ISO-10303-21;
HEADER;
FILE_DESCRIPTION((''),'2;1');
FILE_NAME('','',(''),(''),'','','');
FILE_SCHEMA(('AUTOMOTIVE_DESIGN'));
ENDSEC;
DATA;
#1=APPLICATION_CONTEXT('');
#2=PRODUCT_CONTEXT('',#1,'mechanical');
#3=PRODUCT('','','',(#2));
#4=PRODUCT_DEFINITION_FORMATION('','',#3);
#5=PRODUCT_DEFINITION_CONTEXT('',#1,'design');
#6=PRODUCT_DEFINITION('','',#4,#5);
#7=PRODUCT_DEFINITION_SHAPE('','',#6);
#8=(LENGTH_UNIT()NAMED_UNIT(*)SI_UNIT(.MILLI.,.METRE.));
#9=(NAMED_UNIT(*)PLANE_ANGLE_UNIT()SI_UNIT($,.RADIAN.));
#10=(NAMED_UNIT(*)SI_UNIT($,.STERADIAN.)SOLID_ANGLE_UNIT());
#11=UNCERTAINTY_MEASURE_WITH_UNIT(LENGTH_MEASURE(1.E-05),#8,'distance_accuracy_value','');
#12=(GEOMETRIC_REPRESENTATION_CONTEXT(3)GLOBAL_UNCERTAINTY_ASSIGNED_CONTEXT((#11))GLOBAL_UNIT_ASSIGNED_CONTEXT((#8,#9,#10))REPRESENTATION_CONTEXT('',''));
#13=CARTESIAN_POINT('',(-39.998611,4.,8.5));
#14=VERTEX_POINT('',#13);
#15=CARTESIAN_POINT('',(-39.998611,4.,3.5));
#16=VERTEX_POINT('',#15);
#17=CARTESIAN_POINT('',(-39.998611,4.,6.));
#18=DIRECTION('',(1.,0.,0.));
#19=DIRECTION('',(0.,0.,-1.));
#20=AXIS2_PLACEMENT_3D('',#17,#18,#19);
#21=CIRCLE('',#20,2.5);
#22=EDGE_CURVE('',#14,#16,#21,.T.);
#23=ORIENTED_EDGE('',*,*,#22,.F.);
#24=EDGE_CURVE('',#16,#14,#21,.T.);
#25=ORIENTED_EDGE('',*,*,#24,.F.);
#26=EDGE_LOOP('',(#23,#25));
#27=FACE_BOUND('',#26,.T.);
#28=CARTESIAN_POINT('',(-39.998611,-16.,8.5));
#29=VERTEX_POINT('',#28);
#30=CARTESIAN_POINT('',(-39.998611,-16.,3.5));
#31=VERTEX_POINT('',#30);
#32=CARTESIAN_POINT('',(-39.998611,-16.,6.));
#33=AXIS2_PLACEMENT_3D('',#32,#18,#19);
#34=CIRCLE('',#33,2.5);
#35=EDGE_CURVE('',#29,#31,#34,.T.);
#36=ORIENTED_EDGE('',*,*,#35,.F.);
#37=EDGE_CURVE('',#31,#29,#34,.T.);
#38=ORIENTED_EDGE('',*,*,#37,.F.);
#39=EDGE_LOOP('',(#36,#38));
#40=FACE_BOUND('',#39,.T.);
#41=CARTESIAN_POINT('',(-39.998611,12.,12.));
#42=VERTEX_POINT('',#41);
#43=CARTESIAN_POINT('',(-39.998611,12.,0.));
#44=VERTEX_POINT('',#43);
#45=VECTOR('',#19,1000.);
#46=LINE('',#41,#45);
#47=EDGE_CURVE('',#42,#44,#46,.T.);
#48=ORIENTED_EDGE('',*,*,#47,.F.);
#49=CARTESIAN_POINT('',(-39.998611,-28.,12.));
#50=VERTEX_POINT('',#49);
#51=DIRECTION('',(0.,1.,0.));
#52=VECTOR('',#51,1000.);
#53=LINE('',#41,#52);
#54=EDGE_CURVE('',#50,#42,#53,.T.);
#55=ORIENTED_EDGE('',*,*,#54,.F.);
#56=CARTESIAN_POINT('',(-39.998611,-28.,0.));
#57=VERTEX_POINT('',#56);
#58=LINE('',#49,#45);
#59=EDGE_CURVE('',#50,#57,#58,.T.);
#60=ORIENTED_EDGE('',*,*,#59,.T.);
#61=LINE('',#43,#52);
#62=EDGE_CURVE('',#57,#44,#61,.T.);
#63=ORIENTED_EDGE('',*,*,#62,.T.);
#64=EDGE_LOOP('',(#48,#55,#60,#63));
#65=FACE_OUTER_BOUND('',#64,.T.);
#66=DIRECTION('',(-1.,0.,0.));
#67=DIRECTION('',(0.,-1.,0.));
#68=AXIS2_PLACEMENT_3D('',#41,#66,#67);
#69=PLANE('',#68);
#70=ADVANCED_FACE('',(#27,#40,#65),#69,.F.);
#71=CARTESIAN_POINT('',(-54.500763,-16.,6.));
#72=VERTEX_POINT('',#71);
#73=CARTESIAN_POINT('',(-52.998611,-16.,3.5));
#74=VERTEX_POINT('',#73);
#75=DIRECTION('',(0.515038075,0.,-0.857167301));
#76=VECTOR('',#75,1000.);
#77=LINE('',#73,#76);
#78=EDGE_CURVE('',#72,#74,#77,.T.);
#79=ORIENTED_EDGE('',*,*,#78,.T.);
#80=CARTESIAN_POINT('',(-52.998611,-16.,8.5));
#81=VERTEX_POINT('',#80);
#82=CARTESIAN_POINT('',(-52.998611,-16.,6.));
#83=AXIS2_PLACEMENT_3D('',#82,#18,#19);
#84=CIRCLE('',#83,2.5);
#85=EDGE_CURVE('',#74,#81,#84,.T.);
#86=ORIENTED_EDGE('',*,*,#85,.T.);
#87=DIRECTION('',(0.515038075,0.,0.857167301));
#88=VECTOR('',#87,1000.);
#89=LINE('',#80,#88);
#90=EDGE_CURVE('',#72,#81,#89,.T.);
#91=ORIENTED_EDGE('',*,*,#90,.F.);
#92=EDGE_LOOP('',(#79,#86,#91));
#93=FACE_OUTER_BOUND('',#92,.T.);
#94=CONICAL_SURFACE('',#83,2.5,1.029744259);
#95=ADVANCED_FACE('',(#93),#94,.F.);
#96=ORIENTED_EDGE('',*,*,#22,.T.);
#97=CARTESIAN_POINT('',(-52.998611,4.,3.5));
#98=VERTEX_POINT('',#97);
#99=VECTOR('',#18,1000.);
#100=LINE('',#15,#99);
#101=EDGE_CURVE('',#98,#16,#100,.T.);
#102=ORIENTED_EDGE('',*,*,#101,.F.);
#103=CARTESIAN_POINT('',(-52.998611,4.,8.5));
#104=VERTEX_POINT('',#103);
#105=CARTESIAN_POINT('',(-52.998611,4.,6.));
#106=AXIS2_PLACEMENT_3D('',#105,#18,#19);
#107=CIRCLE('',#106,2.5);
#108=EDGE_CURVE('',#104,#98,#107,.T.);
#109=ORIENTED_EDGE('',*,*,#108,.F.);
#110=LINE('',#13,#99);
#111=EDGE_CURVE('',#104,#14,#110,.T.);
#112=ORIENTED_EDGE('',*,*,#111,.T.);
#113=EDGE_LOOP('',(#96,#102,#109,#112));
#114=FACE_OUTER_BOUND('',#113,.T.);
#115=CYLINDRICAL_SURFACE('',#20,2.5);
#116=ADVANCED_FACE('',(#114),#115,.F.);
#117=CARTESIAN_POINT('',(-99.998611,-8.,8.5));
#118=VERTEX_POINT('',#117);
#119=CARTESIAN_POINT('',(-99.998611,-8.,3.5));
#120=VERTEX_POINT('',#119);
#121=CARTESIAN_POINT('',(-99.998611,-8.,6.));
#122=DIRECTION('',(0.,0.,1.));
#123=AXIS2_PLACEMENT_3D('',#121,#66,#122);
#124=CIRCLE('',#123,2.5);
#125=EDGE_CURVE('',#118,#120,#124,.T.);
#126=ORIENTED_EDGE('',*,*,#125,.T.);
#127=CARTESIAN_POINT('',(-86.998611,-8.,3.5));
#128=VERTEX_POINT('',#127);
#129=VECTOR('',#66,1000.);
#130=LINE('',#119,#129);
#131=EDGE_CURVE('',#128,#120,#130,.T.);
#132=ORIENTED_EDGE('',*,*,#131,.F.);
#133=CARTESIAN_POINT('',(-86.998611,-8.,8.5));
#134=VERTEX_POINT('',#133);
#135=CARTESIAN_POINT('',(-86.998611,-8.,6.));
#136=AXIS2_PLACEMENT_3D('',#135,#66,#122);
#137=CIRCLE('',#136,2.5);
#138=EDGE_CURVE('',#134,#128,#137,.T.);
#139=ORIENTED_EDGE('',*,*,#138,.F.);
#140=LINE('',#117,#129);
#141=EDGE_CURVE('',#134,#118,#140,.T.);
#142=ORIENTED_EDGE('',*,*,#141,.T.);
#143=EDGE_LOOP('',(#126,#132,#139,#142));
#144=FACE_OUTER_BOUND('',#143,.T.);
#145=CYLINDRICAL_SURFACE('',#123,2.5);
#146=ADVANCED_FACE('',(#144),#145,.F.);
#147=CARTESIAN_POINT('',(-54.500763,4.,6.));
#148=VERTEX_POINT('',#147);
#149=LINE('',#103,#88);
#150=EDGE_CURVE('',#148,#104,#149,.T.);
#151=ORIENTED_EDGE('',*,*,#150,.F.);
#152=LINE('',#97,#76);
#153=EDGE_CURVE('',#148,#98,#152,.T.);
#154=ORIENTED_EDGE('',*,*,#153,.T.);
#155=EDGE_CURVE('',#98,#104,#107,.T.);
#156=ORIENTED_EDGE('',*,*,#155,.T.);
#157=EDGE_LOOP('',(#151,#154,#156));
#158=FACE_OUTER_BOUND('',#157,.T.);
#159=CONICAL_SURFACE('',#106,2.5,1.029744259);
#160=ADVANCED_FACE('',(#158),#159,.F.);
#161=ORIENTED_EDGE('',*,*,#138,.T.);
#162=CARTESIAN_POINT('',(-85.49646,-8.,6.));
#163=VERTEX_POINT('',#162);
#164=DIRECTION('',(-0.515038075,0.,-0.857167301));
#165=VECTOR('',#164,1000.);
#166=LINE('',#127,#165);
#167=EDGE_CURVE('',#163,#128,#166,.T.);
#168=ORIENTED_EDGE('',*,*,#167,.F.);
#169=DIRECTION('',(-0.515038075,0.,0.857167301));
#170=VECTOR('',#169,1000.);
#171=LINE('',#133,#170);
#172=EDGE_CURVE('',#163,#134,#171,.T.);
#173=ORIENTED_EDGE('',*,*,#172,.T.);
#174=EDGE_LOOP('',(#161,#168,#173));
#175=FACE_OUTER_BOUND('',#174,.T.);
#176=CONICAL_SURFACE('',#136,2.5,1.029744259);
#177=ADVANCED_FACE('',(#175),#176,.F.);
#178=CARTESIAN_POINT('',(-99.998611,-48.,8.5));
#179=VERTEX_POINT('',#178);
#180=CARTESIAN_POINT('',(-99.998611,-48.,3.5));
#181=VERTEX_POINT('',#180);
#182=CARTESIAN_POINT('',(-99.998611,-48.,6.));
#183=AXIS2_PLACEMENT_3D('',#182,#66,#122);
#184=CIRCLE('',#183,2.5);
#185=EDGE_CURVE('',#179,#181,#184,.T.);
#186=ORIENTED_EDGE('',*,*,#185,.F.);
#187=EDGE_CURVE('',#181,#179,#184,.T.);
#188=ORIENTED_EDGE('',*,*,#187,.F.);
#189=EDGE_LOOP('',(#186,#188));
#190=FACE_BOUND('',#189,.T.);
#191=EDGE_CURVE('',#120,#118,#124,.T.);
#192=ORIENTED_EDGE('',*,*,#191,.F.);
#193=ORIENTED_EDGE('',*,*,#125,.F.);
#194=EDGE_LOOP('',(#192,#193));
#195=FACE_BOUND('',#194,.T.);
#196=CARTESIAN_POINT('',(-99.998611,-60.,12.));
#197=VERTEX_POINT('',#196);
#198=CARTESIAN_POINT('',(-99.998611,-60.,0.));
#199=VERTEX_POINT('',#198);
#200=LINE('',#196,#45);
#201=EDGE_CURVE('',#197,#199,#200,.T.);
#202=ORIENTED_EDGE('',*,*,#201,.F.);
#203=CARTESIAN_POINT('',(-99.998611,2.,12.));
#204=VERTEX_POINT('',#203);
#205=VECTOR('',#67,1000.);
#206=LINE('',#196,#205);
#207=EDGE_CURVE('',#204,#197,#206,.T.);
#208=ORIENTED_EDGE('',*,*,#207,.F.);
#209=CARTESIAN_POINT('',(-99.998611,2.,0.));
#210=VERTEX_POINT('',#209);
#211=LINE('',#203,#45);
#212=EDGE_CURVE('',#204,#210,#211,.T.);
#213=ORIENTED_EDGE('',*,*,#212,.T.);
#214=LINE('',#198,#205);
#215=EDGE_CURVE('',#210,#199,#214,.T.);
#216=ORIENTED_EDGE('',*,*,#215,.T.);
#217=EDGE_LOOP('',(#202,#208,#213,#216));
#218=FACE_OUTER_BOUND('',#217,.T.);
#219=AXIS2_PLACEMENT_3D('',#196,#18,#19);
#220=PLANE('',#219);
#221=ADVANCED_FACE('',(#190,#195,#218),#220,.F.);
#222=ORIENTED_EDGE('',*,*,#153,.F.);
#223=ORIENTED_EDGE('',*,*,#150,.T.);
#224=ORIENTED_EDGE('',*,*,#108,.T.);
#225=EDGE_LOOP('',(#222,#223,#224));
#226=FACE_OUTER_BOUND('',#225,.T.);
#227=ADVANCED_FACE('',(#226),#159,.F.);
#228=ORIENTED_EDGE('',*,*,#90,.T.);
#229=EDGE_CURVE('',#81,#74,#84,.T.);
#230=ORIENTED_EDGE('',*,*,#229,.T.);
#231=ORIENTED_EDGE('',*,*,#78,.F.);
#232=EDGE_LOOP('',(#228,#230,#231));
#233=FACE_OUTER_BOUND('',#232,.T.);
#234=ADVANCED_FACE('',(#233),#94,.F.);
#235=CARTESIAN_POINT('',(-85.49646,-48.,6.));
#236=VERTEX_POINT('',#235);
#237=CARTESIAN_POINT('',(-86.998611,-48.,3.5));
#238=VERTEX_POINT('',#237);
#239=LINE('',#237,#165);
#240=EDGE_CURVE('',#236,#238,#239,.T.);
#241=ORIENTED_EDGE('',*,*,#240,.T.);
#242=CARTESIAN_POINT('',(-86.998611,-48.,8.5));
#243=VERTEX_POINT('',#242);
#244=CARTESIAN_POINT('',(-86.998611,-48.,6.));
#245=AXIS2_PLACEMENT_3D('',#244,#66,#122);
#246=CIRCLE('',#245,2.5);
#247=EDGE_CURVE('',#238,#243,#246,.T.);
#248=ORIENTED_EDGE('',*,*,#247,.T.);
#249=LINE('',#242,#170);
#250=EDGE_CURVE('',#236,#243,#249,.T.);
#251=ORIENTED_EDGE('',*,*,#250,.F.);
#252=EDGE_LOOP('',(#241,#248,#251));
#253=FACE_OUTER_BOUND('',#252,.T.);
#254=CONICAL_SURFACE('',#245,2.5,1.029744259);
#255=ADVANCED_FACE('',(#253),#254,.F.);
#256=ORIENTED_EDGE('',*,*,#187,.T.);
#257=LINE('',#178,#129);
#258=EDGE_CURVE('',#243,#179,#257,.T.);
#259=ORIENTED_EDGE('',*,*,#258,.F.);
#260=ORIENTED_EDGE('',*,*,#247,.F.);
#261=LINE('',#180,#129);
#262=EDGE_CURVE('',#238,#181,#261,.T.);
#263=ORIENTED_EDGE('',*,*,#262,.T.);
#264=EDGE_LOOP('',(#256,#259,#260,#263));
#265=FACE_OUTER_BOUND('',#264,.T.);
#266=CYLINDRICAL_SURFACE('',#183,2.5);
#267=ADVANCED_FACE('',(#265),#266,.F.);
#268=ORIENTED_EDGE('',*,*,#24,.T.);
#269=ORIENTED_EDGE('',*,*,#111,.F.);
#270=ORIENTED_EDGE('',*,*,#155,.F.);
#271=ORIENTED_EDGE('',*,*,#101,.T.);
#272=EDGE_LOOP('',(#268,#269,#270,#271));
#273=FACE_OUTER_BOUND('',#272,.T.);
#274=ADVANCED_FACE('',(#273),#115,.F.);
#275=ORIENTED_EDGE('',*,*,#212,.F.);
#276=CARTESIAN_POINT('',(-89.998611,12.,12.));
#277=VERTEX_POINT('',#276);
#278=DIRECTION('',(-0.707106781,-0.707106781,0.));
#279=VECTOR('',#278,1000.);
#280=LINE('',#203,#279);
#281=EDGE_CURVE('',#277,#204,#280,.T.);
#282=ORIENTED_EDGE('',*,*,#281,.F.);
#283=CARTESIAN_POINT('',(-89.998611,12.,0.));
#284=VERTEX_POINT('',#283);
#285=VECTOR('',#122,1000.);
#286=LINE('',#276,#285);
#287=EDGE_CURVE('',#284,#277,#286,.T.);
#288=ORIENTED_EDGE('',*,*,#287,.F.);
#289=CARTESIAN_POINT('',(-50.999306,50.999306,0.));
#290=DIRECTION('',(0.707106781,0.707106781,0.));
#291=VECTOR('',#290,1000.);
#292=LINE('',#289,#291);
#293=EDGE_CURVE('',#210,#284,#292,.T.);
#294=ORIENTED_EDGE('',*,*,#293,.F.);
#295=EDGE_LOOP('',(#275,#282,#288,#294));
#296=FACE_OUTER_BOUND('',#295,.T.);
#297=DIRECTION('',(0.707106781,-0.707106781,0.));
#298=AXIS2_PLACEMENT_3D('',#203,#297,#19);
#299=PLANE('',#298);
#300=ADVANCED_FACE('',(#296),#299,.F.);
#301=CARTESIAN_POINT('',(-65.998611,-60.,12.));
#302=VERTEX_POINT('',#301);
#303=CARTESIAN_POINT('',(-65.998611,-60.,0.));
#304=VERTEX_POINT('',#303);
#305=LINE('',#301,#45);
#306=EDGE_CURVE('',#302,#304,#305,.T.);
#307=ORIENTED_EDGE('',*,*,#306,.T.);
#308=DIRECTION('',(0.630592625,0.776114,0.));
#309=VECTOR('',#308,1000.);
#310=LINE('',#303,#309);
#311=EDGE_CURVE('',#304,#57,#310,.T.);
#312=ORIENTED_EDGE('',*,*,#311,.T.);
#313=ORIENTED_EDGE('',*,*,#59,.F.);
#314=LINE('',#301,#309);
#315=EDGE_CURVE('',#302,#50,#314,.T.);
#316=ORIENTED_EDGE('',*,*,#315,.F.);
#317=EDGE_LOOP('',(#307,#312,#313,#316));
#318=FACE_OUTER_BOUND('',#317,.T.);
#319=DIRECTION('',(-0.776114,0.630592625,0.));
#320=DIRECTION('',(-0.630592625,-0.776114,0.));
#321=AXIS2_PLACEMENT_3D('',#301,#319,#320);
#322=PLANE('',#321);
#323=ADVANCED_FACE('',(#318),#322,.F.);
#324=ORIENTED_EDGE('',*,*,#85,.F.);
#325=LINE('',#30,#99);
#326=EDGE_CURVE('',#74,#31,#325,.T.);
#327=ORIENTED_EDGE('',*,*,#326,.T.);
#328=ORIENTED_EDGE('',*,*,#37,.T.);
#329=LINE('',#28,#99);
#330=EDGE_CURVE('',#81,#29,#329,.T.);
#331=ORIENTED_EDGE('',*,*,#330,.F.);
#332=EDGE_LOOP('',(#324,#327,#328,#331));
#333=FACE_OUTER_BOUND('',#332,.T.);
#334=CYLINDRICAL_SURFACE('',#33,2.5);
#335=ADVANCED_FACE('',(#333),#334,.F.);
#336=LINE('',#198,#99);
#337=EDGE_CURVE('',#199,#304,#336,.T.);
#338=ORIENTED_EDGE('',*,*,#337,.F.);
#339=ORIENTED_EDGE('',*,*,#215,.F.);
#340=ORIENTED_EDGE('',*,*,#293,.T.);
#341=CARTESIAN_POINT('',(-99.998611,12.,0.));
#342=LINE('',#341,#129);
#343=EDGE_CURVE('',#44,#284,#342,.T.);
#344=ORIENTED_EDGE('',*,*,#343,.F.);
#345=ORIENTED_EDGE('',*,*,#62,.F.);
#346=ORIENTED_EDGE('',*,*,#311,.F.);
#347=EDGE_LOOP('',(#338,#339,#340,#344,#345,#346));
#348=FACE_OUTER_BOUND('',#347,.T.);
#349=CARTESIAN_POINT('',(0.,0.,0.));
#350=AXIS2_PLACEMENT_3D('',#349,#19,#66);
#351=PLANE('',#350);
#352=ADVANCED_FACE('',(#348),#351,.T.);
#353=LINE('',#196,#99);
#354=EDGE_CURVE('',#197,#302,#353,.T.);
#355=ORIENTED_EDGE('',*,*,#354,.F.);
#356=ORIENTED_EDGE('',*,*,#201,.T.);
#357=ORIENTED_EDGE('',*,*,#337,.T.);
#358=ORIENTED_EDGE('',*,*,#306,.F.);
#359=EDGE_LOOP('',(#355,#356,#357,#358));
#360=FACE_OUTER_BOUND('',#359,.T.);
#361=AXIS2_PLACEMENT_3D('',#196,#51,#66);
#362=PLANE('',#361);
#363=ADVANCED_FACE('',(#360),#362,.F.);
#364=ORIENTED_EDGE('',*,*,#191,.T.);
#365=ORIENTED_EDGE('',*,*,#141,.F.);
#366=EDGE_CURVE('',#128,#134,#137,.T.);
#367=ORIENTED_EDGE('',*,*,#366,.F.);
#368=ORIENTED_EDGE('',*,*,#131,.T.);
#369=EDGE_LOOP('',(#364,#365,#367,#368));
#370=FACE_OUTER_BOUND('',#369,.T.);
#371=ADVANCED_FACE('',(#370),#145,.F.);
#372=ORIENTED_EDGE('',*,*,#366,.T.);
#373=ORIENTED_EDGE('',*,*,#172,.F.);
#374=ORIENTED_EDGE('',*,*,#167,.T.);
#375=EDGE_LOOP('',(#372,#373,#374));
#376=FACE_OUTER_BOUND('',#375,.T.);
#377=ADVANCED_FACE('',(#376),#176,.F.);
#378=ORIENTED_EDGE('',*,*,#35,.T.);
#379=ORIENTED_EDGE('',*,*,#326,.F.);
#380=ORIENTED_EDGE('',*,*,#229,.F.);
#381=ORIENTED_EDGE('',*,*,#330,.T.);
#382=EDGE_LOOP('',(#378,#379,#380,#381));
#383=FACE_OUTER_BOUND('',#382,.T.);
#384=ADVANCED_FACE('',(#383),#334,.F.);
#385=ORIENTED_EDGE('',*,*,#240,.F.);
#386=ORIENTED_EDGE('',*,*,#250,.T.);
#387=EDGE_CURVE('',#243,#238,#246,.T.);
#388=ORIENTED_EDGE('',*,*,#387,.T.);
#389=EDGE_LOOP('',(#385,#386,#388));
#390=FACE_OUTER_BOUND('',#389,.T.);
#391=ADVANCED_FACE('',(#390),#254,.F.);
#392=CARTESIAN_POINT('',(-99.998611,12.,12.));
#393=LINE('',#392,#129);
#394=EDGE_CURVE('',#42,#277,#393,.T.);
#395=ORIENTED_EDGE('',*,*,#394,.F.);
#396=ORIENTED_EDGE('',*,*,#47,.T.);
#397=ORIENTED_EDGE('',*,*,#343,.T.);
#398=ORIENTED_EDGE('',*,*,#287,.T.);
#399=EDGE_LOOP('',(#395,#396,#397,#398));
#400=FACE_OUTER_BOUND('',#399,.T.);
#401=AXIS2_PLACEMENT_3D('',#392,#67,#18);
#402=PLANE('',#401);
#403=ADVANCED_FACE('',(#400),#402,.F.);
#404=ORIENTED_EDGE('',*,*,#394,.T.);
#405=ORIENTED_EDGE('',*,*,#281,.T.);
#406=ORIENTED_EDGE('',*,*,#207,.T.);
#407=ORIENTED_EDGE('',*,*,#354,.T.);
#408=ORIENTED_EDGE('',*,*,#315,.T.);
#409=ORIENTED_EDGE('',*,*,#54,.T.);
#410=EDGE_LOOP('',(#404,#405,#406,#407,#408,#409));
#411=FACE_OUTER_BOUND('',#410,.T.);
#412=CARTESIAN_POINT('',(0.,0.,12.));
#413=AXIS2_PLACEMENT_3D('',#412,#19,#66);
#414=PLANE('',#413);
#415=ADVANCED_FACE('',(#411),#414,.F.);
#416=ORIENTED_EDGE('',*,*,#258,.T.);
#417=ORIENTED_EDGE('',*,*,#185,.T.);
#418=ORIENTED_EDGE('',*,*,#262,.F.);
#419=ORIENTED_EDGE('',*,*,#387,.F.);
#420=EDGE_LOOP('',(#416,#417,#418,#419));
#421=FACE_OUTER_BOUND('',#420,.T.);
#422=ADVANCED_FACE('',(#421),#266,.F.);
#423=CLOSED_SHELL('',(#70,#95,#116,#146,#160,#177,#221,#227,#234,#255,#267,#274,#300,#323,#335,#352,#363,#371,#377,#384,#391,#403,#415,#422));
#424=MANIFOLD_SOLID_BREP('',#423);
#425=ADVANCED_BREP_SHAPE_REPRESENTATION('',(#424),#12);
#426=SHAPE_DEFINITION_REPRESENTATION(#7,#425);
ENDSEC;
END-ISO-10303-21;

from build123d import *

# Parameters (mm, degrees)
EXTRUDE_1_DEPTH        = 12
CHAMFER_1_SIZE         = 10
HOLE_WIZARD_M6_1_D     = 5
HOLE_WIZARD_M6_1_DEPTH = 13
HOLE_WIZARD_M6_1_TIP   = 1.502151548
HOLE_WIZARD_M6_2_D     = 5
HOLE_WIZARD_M6_2_DEPTH = 13
HOLE_WIZARD_M6_2_TIP   = 1.502151548


with BuildPart() as part:
    # 草图1 → 凸台-拉伸1 (new body)
    with BuildSketch(Plane.XY):
        Polygon((-39.998611317, 12), (-39.998611317, -28), (-65.998611317, -60), (-99.998611317, -60), (-99.998611317, 12), align=None)
    extrude(amount=EXTRUDE_1_DEPTH)

    # 倒角1
    chamfer_1_edges = [part.edges().sort_by_distance(p)[0] for p in [
        (-99.998611317, 12, 6),
    ]]
    chamfer(chamfer_1_edges, length=CHAMFER_1_SIZE)

    # M6 螺纹孔1
    with Locations(Plane(origin=(-39.998611317, 0, 0), x_dir=(0, 0, -1), z_dir=(1, 0, 0))):
        with Locations((-6, 4), (-6, -16)):
            Hole(HOLE_WIZARD_M6_1_D / 2, depth=HOLE_WIZARD_M6_1_DEPTH)
            with Locations((0, 0, -(HOLE_WIZARD_M6_1_DEPTH + HOLE_WIZARD_M6_1_TIP / 2))):  # 118° drill point
                Cone(0, HOLE_WIZARD_M6_1_D / 2, HOLE_WIZARD_M6_1_TIP, mode=Mode.SUBTRACT)

    # M6 螺纹孔2
    with Locations(Plane.ZY.offset(99.998611317)):
        with Locations((6, -8), (6, -48)):
            Hole(HOLE_WIZARD_M6_2_D / 2, depth=HOLE_WIZARD_M6_2_DEPTH)
            with Locations((0, 0, -(HOLE_WIZARD_M6_2_DEPTH + HOLE_WIZARD_M6_2_TIP / 2))):  # 118° drill point
                Cone(0, HOLE_WIZARD_M6_2_D / 2, HOLE_WIZARD_M6_2_TIP, mode=Mode.SUBTRACT)


solid = part.part
